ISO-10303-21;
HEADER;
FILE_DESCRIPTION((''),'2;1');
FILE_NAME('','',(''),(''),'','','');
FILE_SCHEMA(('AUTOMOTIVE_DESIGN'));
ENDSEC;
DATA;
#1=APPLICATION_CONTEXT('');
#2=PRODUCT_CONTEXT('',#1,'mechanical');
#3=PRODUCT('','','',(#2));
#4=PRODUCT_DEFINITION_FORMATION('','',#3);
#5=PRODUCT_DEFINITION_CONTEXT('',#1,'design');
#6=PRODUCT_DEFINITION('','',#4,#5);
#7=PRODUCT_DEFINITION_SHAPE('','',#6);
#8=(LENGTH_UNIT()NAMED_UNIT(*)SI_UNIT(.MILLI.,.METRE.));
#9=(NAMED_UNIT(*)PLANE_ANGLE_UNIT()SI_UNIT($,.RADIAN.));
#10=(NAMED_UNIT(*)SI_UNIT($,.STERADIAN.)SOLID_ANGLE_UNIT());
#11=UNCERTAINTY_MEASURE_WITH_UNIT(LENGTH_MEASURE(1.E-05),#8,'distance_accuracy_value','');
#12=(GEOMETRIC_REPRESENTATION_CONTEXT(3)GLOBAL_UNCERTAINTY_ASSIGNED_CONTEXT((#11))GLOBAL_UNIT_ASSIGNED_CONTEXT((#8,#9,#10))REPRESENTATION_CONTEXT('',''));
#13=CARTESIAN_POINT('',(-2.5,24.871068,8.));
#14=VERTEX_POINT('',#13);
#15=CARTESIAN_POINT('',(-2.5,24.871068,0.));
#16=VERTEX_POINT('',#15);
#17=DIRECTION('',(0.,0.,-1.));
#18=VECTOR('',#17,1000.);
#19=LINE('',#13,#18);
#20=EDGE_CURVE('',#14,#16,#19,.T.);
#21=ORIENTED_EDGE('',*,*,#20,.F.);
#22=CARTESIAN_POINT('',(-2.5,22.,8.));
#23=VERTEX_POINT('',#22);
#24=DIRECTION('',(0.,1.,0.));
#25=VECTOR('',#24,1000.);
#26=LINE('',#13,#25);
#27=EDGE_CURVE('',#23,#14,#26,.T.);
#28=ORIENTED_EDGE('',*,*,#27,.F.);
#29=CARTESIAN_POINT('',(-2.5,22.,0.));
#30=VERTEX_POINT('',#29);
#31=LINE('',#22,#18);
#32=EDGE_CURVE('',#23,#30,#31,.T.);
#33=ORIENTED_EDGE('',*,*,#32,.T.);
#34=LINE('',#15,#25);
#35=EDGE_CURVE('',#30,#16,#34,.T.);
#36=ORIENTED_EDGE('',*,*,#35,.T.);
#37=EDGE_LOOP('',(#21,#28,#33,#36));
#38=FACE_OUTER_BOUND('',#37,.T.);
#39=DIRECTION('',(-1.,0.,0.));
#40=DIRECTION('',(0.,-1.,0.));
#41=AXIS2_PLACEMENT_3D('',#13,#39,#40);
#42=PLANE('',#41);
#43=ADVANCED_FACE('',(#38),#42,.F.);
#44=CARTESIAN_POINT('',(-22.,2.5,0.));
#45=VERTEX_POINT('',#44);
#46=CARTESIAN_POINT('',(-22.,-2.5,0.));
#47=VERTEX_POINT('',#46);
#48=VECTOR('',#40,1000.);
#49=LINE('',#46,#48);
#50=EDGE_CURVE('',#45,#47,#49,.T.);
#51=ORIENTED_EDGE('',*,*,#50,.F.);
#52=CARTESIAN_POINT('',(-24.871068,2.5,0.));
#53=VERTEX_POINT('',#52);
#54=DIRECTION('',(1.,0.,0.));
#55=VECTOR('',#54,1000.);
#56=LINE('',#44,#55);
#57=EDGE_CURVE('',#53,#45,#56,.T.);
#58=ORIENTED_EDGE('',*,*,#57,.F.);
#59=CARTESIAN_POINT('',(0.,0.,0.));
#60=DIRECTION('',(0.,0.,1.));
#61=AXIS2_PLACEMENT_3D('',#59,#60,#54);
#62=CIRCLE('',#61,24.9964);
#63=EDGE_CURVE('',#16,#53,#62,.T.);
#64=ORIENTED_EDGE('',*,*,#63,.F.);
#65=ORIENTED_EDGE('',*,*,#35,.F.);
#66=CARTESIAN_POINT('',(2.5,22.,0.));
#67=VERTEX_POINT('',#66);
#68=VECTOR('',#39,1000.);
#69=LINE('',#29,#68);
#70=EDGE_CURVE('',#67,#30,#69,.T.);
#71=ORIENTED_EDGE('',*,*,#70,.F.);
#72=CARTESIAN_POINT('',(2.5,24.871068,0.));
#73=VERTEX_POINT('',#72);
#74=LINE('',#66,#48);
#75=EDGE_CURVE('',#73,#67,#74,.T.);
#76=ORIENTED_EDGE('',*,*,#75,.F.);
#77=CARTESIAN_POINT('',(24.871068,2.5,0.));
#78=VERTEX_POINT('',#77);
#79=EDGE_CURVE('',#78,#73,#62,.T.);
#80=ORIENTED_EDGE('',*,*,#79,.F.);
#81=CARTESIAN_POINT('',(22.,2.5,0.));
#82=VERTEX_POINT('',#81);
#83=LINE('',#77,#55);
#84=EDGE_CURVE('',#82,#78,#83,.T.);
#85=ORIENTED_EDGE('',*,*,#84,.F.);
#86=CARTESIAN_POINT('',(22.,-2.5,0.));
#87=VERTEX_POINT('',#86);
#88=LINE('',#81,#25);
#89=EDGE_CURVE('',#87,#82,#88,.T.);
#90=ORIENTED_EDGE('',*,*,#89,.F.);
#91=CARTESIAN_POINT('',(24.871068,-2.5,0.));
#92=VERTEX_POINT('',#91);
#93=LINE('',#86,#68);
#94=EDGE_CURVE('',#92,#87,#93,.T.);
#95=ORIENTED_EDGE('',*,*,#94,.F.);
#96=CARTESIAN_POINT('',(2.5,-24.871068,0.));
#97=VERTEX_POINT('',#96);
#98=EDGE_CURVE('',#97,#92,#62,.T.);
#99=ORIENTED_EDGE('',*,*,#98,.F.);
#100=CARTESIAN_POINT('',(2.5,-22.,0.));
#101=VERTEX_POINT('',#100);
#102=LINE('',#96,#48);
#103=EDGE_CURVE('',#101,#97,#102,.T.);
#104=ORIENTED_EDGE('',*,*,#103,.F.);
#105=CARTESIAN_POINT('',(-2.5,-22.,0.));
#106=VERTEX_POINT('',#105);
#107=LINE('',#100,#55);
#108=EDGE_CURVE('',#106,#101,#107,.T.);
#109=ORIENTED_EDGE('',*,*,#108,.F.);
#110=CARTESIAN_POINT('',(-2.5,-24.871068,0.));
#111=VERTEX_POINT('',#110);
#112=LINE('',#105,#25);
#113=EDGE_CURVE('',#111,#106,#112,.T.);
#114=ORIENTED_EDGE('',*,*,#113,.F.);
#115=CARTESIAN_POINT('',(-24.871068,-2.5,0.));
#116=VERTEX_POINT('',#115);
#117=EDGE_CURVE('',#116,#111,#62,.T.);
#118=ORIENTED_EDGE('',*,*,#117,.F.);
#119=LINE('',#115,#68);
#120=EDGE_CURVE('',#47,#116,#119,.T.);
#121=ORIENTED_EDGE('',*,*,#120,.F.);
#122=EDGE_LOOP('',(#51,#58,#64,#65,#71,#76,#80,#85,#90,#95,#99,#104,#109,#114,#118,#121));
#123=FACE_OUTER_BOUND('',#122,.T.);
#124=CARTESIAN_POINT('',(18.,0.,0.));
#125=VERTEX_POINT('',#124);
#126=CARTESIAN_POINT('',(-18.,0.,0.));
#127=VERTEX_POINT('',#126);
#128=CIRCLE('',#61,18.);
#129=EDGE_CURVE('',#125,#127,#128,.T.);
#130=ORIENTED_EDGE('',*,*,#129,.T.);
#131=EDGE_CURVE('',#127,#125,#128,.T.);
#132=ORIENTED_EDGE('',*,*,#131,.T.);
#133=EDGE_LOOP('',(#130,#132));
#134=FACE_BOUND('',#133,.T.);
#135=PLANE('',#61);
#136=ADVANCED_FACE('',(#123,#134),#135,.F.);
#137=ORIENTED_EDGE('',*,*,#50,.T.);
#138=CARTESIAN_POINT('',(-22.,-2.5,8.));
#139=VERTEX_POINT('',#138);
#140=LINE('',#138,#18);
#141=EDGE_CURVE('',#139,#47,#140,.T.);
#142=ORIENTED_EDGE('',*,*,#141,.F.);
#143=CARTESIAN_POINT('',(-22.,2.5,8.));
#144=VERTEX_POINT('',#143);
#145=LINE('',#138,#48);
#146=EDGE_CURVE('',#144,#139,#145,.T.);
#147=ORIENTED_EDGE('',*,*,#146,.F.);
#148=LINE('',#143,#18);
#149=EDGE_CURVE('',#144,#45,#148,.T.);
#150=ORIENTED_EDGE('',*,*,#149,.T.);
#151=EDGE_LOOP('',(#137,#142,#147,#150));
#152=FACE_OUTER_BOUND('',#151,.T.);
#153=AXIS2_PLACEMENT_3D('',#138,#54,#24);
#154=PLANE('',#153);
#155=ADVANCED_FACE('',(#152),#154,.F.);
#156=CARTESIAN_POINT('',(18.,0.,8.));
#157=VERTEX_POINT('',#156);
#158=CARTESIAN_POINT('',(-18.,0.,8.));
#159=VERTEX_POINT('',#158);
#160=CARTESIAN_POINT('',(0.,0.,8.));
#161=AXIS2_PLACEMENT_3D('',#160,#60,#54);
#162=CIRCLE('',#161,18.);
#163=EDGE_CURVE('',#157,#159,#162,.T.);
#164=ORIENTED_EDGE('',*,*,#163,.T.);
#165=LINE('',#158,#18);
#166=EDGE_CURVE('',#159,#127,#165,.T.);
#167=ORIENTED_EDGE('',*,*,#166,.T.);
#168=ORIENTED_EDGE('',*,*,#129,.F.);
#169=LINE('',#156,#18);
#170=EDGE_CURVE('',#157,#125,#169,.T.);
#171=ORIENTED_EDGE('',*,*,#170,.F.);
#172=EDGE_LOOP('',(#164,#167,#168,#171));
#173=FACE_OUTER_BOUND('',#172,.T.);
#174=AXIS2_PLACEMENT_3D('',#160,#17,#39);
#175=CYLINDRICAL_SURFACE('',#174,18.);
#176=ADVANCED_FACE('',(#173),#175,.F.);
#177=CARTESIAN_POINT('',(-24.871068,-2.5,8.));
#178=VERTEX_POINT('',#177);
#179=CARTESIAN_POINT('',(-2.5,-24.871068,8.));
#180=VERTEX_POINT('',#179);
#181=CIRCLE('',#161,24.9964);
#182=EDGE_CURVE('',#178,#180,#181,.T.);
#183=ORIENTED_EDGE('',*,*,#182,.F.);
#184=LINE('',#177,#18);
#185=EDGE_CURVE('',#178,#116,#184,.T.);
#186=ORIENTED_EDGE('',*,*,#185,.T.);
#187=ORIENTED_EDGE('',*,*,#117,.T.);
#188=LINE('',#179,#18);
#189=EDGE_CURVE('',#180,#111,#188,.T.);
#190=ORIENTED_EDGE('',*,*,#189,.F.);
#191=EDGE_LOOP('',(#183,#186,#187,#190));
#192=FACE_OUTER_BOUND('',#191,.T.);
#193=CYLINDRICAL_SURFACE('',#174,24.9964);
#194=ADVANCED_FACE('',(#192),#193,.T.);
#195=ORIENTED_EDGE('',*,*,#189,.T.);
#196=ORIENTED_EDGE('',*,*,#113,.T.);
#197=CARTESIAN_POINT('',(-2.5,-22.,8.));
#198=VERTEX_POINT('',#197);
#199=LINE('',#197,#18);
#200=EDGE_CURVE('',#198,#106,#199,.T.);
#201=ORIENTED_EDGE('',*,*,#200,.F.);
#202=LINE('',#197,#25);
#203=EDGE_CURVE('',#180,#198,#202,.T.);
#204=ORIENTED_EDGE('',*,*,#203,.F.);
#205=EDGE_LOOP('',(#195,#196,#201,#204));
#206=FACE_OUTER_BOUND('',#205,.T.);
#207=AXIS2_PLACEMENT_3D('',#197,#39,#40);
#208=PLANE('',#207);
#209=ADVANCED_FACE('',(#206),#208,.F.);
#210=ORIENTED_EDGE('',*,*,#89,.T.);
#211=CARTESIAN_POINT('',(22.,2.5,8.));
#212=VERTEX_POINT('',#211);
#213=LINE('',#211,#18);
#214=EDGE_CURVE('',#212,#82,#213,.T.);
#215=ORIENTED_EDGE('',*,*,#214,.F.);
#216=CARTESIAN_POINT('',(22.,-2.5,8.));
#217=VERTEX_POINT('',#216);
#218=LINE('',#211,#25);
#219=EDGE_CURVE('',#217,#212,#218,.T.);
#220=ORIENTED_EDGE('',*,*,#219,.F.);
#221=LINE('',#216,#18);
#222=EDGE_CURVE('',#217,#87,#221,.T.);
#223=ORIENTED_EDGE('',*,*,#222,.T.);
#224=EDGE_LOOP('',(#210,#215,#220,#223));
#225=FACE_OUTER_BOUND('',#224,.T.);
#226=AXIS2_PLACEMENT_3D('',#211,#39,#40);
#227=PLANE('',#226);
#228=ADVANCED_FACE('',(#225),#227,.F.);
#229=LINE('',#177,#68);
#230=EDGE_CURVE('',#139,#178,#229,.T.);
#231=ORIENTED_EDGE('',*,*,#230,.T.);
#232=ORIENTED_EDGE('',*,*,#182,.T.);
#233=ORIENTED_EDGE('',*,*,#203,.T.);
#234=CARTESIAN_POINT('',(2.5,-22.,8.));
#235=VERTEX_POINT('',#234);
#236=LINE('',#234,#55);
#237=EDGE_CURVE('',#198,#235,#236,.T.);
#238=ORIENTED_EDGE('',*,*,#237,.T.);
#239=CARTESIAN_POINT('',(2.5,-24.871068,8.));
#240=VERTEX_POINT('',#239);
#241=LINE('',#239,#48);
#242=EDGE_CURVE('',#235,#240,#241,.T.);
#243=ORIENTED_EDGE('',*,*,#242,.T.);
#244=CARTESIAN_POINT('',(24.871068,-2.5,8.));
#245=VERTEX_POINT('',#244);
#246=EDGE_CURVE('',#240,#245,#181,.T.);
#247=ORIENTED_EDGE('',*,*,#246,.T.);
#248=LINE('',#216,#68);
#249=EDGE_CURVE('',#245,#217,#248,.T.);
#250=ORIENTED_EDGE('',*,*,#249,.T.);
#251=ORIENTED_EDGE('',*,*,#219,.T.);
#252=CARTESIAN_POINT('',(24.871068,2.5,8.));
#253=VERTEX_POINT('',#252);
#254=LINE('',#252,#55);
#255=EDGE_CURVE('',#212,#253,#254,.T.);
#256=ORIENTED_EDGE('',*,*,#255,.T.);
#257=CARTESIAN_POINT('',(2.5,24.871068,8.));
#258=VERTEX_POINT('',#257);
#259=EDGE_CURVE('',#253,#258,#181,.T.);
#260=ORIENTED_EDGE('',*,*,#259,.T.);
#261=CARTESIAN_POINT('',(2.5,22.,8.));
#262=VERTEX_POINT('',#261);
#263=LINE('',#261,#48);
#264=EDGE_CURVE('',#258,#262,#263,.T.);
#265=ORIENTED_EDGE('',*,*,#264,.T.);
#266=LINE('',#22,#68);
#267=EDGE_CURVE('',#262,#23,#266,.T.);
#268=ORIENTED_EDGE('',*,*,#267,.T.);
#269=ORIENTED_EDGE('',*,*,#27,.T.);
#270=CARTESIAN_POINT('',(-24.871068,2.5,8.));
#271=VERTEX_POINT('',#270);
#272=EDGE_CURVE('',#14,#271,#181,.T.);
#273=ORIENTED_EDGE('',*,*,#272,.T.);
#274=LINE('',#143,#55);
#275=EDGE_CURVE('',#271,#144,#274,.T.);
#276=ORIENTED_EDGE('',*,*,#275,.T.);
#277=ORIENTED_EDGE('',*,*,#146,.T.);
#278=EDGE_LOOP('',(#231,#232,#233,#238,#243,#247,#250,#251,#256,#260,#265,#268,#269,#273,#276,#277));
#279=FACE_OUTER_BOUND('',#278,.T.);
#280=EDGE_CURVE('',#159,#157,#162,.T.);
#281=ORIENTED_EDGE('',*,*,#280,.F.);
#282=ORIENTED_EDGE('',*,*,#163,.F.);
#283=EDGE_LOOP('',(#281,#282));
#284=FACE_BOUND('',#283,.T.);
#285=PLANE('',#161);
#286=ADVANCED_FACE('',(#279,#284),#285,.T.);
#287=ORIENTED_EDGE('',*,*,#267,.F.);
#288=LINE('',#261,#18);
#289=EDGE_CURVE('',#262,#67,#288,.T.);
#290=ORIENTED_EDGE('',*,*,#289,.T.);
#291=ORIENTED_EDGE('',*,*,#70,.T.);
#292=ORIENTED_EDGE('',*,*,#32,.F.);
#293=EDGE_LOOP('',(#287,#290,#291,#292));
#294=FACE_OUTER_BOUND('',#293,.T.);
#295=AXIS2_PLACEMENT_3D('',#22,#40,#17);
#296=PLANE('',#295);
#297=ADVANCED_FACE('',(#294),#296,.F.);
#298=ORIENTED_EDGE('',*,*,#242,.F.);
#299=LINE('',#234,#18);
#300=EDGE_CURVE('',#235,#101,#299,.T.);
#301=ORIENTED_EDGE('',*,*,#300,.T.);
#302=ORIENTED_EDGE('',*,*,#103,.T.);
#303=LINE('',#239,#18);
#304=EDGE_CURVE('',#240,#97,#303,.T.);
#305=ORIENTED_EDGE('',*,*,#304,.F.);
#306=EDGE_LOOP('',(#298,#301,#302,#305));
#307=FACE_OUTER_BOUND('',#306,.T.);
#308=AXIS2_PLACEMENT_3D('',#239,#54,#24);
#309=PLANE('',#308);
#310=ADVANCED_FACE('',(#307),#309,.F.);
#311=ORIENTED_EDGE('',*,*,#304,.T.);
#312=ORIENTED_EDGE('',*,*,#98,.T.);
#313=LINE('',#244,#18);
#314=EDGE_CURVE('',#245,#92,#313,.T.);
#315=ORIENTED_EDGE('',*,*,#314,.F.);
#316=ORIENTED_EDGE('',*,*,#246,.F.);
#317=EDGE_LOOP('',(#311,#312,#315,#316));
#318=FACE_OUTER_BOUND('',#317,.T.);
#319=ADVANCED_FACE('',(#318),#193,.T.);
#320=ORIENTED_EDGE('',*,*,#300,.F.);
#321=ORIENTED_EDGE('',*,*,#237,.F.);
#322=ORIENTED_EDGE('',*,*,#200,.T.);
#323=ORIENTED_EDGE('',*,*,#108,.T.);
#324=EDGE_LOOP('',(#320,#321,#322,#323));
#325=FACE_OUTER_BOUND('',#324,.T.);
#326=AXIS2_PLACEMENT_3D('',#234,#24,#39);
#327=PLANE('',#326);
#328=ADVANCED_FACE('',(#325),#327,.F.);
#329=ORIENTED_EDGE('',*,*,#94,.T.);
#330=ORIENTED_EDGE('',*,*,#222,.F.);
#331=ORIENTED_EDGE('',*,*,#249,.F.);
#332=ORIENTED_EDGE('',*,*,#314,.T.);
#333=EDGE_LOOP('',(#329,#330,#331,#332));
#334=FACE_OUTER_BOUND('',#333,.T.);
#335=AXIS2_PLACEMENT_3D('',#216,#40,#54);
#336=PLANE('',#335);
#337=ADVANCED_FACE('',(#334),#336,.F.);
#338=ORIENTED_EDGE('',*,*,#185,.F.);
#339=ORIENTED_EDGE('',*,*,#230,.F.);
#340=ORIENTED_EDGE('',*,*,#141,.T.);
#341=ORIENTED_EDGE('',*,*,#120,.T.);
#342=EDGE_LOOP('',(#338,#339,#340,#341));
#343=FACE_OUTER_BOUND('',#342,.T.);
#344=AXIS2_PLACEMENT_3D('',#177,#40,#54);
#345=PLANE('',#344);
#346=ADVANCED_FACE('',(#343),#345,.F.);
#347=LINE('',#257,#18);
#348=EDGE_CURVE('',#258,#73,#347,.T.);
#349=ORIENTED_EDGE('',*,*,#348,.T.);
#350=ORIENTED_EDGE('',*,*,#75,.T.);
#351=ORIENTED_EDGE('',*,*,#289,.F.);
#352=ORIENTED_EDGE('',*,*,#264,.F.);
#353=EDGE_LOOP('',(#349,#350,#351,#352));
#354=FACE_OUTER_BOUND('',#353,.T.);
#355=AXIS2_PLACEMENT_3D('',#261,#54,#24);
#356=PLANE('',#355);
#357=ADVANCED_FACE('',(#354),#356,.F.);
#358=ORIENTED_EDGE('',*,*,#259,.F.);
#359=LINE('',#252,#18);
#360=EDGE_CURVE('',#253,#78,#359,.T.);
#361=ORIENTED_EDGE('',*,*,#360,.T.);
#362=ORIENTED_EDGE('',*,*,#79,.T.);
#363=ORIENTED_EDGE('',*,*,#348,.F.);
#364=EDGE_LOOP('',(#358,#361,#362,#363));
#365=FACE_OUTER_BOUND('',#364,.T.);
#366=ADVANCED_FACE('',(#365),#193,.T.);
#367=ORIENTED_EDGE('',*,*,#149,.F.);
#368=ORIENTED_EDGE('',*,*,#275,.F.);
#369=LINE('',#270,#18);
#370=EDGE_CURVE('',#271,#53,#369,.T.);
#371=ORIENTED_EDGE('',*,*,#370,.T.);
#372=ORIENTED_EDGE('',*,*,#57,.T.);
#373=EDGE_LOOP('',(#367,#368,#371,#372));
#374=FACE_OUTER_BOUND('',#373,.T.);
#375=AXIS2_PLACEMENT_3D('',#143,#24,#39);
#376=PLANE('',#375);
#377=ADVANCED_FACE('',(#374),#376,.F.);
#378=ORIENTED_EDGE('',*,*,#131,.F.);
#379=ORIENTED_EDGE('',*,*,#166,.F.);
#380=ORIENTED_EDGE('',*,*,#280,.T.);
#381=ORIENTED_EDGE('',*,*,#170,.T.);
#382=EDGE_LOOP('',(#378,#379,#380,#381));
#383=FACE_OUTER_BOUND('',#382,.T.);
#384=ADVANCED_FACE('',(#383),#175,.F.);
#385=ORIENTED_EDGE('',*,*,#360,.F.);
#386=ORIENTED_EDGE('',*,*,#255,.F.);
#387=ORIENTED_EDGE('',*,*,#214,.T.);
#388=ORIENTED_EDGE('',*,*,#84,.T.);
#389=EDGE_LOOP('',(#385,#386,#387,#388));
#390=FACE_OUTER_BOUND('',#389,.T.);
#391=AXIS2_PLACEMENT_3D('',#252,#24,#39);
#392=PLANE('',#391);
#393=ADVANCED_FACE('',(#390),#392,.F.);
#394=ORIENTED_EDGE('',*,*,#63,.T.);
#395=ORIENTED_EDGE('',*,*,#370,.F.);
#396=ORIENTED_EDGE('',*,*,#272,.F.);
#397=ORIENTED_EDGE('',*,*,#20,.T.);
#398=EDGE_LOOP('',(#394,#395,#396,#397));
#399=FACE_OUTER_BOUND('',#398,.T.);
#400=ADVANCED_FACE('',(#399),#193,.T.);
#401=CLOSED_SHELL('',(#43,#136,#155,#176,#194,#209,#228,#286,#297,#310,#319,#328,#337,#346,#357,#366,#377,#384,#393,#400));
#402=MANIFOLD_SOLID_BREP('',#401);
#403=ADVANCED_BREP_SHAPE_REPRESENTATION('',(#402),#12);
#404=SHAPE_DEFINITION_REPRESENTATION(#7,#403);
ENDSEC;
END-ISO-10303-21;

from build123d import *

# Parameters (mm, degrees)
SKETCH_1_R      = 18
EXTRUDE_1_DEPTH = 8


with BuildPart() as part:
    # 草图1 → 拉伸1 (new body)
    with BuildSketch(Plane.XY):
        with BuildLine():
            Line((-2.5, 24.871068248), (-2.5, 22))
            Line((-2.5, 22), (2.5, 22))
            Line((2.5, 22), (2.5, 24.871068248))
            ThreePointArc((2.5, 24.871068248), (17.675124268, 17.675124268), (24.871068248, 2.5))
            Line((24.871068248, 2.5), (22, 2.5))
            Line((22, 2.5), (22, -2.5))
            Line((22, -2.5), (24.871068248, -2.5))
            ThreePointArc((24.871068248, -2.5), (17.675124268, -17.675124268), (2.5, -24.871068248))
            Line((2.5, -24.871068248), (2.5, -22))
            Line((2.5, -22), (-2.5, -22))
            Line((-2.5, -22), (-2.5, -24.871068248))
            ThreePointArc((-2.5, -24.871068248), (-17.675124268, -17.675124268), (-24.871068248, -2.5))
            Line((-24.871068248, -2.5), (-22, -2.5))
            Line((-22, -2.5), (-22, 2.5))
            Line((-22, 2.5), (-24.871068248, 2.5))
            ThreePointArc((-24.871068248, 2.5), (-17.675124268, 17.675124268), (-2.5, 24.871068248))
        make_face()
        Circle(SKETCH_1_R, mode=Mode.SUBTRACT)
    extrude(amount=EXTRUDE_1_DEPTH)


solid = part.part
